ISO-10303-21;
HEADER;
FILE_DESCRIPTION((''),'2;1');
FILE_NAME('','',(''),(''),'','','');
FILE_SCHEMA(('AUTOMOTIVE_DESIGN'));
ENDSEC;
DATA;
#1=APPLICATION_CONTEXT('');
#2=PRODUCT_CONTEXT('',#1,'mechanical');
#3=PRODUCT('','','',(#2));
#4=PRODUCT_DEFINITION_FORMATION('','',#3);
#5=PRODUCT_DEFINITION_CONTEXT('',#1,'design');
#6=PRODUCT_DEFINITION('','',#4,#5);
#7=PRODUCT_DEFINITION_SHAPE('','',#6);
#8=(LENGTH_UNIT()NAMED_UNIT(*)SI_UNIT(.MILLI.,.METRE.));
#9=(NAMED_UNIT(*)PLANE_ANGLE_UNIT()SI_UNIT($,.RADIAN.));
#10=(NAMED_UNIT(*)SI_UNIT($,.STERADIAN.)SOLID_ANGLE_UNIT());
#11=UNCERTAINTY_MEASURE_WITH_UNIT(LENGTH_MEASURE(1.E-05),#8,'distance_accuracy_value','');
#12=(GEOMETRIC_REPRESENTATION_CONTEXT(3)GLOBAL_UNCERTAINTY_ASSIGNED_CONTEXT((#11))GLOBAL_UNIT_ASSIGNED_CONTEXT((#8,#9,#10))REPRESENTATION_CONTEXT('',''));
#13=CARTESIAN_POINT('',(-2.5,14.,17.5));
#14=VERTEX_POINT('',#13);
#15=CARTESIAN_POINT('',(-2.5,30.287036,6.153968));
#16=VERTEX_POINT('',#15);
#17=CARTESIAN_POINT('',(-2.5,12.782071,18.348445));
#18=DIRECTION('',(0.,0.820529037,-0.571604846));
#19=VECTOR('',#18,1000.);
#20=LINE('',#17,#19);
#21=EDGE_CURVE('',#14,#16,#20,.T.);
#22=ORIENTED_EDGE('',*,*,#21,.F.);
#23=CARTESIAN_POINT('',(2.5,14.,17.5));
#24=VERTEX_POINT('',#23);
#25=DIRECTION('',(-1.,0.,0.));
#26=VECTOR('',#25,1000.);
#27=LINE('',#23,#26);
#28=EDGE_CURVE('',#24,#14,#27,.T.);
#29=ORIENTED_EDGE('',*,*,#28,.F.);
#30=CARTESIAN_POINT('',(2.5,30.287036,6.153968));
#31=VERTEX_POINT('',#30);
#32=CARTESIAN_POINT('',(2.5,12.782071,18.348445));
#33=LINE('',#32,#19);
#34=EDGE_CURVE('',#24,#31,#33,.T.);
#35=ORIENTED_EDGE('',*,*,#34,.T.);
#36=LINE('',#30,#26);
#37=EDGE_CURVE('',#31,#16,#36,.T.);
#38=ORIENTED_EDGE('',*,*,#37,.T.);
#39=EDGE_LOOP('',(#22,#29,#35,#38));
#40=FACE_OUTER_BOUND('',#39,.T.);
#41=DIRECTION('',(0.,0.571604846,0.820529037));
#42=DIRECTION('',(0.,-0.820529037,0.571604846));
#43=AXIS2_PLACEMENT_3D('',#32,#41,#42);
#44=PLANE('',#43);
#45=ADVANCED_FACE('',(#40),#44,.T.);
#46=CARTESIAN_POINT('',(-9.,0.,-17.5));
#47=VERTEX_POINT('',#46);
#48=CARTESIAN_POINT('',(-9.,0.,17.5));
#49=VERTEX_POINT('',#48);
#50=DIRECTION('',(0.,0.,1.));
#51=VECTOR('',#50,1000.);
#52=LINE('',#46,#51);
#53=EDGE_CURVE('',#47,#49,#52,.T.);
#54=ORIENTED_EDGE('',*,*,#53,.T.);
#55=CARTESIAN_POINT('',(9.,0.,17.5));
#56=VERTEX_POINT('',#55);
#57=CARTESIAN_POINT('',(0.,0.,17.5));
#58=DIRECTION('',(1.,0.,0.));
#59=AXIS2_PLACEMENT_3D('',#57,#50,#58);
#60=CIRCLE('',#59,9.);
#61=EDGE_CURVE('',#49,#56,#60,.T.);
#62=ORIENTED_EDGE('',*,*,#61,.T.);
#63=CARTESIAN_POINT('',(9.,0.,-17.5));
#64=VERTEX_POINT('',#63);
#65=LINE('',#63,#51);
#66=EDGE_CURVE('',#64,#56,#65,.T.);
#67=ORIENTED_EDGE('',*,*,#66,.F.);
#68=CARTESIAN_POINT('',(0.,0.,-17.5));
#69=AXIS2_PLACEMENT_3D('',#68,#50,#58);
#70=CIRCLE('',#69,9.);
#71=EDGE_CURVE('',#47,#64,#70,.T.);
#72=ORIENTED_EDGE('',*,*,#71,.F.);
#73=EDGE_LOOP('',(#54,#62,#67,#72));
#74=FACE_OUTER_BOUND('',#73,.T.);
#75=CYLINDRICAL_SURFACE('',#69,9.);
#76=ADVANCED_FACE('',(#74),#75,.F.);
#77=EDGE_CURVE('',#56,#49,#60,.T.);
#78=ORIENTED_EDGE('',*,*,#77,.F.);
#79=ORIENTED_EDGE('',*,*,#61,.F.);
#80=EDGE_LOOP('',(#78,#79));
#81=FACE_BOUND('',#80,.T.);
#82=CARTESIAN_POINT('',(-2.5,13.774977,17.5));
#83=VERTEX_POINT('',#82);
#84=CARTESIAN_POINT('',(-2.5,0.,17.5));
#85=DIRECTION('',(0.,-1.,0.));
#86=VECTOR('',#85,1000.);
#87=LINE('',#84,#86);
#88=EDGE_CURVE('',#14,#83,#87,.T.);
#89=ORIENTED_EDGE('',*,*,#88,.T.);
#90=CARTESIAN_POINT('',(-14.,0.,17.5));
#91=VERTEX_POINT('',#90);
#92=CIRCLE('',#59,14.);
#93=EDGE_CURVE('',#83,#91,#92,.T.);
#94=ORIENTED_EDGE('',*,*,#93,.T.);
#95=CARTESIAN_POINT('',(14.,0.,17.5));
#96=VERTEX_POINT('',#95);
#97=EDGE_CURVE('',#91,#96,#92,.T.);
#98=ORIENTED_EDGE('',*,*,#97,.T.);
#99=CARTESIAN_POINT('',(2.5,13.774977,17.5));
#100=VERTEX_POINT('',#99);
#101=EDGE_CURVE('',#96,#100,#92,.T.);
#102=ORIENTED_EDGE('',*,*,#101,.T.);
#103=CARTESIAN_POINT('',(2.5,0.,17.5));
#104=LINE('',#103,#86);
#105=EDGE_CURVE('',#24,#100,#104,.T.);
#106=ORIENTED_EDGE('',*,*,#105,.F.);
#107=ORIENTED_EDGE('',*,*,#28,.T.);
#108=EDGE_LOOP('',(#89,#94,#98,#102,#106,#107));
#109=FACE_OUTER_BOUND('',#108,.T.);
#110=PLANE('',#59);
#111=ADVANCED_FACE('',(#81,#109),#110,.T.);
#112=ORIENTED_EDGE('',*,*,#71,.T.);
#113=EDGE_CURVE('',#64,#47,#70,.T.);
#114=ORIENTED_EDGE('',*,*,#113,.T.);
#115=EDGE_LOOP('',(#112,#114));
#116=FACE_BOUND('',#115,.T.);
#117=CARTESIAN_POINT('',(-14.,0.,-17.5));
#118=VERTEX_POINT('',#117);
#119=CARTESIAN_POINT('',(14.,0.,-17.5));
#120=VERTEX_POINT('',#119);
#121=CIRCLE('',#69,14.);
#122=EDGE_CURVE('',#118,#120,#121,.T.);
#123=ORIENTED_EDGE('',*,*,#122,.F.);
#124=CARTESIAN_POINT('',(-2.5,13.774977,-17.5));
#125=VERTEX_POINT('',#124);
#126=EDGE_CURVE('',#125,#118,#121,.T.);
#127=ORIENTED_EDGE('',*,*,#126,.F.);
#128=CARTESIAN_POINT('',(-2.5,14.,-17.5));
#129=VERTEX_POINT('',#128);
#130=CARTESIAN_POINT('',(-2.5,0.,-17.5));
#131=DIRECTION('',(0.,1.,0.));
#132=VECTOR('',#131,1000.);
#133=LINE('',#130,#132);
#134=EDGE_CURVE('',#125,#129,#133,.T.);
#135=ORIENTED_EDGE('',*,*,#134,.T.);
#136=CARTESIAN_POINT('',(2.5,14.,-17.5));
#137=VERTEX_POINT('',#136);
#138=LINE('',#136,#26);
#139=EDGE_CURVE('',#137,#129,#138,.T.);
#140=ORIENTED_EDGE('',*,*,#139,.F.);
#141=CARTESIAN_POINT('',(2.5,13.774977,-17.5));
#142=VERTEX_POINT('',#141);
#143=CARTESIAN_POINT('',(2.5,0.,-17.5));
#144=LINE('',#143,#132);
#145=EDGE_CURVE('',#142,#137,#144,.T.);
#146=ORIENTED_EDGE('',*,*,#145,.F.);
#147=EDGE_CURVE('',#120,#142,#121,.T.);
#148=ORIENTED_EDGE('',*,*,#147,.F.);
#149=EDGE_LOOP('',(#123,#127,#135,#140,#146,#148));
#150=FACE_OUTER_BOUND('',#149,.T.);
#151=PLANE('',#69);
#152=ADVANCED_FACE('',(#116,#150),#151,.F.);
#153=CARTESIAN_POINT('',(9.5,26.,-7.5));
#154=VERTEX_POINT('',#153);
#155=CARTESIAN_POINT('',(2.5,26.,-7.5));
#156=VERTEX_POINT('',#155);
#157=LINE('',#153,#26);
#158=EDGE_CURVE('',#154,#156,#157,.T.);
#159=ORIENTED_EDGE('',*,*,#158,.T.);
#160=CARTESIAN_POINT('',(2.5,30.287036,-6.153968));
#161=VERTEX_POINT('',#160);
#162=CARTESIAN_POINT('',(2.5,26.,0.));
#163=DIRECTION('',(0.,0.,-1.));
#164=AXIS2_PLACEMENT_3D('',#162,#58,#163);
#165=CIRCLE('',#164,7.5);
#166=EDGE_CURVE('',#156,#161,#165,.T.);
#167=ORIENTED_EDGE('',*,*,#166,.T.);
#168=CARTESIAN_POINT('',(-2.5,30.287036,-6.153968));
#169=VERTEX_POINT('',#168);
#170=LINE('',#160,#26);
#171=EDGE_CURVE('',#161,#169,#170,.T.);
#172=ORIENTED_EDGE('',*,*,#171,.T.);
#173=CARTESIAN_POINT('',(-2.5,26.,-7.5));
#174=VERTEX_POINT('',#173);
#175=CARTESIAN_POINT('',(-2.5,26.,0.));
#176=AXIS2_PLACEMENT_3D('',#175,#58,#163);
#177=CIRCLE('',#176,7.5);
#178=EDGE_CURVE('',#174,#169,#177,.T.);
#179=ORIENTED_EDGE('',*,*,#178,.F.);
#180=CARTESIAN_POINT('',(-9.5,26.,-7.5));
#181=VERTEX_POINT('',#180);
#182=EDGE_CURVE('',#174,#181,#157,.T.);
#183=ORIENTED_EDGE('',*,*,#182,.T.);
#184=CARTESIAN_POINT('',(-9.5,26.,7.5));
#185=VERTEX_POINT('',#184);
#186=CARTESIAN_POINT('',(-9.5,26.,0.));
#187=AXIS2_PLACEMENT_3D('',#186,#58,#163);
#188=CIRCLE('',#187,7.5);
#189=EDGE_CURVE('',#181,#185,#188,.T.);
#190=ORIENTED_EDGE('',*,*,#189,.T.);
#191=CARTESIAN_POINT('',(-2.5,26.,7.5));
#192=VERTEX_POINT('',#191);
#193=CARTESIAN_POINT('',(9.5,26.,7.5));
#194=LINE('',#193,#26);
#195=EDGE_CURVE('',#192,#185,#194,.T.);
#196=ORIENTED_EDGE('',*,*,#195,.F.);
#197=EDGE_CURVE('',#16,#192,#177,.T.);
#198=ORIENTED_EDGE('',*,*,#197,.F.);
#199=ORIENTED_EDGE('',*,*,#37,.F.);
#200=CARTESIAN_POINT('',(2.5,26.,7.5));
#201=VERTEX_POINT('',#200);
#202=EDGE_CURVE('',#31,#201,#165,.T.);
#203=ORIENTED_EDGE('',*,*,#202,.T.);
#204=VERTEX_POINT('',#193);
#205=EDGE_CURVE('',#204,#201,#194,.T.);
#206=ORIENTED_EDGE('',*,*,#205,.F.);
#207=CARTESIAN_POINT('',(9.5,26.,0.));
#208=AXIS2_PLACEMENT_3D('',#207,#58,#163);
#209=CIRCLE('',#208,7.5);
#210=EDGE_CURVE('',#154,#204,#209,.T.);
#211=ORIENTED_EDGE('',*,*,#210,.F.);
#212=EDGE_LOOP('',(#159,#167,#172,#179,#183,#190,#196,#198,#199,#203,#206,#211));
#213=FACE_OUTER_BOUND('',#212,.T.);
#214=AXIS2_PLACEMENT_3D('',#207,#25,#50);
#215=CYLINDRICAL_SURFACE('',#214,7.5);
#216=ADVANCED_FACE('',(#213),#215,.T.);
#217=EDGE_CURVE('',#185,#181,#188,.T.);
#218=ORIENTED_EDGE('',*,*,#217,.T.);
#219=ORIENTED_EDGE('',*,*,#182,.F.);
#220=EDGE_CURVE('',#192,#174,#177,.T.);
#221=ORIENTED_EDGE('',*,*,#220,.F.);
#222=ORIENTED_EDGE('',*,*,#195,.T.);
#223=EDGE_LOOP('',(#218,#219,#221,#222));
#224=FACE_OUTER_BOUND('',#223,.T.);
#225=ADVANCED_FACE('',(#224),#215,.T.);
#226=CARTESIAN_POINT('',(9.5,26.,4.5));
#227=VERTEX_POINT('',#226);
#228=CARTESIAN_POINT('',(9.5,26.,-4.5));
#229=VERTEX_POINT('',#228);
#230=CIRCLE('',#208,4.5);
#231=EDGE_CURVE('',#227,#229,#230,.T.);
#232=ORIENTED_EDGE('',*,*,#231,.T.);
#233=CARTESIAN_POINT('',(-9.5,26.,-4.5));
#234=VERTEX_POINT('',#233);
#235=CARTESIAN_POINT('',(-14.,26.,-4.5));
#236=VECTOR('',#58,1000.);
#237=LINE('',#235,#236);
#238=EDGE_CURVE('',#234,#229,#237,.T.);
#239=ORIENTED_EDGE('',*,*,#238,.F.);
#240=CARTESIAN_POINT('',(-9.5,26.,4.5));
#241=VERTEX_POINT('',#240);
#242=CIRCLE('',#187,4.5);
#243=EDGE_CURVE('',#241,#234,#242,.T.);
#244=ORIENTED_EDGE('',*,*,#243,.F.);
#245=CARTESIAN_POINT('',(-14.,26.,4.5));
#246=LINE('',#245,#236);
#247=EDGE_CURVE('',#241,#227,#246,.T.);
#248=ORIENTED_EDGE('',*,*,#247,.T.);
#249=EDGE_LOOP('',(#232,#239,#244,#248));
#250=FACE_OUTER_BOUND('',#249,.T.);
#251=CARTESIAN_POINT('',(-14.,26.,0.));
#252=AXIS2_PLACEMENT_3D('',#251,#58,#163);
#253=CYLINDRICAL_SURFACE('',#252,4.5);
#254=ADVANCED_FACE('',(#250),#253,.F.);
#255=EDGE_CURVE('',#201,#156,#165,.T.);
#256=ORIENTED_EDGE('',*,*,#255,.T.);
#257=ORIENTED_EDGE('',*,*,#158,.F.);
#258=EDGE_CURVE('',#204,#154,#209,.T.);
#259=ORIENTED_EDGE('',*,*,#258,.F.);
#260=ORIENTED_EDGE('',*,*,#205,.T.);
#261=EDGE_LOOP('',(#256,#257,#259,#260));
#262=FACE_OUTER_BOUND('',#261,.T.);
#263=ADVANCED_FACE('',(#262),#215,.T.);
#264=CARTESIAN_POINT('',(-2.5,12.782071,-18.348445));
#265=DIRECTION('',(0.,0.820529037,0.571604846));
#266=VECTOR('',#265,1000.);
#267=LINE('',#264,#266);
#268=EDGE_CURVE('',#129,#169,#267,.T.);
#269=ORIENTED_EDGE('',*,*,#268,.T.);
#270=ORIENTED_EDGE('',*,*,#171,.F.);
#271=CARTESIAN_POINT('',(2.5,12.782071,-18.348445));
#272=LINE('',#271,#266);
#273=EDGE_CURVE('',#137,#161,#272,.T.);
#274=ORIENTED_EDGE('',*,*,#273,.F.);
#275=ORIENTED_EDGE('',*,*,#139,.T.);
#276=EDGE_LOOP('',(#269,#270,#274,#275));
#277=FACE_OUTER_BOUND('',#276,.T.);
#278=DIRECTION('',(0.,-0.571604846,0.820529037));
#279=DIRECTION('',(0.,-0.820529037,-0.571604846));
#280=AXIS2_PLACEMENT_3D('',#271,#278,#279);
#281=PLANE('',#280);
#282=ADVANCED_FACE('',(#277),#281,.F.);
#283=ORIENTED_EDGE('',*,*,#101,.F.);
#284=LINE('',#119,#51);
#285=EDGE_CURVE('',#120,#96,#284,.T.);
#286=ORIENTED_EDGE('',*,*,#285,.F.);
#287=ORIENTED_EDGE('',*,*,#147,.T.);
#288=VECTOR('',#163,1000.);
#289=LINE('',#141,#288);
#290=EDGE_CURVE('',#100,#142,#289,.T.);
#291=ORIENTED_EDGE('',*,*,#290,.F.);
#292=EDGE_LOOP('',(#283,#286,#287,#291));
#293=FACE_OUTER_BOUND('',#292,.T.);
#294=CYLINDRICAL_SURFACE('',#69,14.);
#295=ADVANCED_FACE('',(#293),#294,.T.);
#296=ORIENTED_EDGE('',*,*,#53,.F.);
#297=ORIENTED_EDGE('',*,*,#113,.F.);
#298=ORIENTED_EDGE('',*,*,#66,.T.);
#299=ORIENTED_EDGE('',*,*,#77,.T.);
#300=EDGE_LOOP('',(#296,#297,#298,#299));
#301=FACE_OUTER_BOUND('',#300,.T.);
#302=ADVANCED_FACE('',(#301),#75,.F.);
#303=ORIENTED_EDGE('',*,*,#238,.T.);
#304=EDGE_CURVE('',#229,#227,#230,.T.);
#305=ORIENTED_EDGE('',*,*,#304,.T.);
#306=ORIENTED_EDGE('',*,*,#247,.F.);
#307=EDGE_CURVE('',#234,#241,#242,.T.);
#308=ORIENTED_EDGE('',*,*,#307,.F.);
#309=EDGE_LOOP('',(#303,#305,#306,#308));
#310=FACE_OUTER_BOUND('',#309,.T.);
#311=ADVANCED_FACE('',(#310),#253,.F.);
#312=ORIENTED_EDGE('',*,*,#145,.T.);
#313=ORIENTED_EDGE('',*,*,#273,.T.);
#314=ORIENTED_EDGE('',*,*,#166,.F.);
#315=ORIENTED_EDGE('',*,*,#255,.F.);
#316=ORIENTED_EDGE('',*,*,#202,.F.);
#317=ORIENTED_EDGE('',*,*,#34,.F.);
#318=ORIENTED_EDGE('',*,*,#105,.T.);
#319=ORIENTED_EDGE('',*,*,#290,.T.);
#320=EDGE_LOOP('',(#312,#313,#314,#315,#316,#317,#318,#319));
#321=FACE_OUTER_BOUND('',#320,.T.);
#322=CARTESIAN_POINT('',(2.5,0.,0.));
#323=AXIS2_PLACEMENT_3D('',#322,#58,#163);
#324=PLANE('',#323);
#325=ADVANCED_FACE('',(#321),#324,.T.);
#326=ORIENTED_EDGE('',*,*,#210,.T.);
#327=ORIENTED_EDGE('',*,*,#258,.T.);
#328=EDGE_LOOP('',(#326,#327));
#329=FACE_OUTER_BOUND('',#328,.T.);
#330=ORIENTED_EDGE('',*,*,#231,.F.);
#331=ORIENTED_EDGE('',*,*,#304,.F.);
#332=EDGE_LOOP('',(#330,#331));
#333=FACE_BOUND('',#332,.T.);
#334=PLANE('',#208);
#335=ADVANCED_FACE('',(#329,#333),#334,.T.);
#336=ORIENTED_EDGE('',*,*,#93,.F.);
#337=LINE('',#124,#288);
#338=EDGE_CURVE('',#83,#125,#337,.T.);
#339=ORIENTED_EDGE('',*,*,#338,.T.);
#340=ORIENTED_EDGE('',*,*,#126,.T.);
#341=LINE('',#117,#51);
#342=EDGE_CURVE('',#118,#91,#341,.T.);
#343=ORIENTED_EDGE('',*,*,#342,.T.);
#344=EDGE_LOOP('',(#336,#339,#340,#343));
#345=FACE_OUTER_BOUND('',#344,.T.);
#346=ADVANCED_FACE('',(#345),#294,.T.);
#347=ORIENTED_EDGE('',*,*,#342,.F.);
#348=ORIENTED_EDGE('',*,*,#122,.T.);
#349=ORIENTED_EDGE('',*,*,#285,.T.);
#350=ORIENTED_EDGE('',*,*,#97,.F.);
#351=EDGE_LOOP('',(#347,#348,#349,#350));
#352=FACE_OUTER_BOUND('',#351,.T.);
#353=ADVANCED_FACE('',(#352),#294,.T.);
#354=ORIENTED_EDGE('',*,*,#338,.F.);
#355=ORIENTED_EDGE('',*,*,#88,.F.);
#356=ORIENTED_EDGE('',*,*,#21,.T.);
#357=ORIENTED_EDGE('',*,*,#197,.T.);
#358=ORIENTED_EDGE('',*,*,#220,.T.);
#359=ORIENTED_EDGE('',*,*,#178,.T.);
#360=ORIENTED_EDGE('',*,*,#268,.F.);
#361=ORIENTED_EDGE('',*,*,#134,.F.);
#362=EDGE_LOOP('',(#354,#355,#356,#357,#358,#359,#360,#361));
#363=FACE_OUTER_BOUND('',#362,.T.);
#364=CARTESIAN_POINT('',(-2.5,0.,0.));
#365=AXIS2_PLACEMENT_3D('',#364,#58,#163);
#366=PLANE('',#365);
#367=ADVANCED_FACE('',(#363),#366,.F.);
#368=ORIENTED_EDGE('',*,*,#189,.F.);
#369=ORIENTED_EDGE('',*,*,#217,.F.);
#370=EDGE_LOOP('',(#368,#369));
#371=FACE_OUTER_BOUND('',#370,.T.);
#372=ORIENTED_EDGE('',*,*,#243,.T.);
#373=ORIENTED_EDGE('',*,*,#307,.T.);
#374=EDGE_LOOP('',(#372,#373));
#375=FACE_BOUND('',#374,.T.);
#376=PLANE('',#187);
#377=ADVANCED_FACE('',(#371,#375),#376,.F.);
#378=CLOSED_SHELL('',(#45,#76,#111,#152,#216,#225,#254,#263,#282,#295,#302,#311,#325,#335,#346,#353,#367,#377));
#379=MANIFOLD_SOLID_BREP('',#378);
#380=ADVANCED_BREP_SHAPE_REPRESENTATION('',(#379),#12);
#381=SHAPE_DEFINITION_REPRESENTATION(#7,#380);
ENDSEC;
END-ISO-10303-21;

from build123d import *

# Parameters (mm, degrees)
MAIN_BARREL_28_DEPTH      = 17.5
MAIN_BARREL_28_DEPTH_BACK = 17.5
MAIN_BARREL_SKETCH_R      = 14
MAIN_BORE_SKETCH_R        = 9
MAIN_BORE_18_DEPTH        = 41.211938526
UPPER_BOSS_SKETCH_R       = 7.5
UPPER_BOSS_15_DEPTH       = 9.5
UPPER_BORE_SKETCH_R       = 4.5
UPPER_BORE_9_DEPTH        = 45.505617623
CONNECTING_WEB_DEPTH      = 2.5


with BuildPart() as part:
    # Main Barrel Sketch → Main Barrel _28 (new, two sides: drawn at the far end of the back side and taken through both)
    with BuildSketch(Plane.XY.offset(-MAIN_BARREL_28_DEPTH_BACK)):
        Circle(MAIN_BARREL_SKETCH_R)
    extrude(amount=MAIN_BARREL_28_DEPTH + MAIN_BARREL_28_DEPTH_BACK)

    # Main Bore Sketch → Main Bore _18 (cut, through all)
    with BuildSketch(Plane.XY.offset(17.5)):
        Circle(MAIN_BORE_SKETCH_R)
    extrude(amount=-MAIN_BORE_18_DEPTH, mode=Mode.SUBTRACT)



with BuildPart() as body_2:
    # Upper Boss Sketch → Upper Boss _15 (new, symmetric)
    with BuildSketch(Plane(origin=(0, 0, 0), x_dir=(0, 0, -1), z_dir=(1, 0, 0))):
        with Locations((0, 26)):
            Circle(UPPER_BOSS_SKETCH_R)
    extrude(amount=UPPER_BOSS_15_DEPTH, both=True)

    # Upper Bore Sketch → Upper Bore _9 (cut, through all)
    with BuildSketch(Plane(origin=(9.5, 0, 0), x_dir=(0, 0, -1), z_dir=(1, 0, 0))):
        with Locations((0, 26)):
            Circle(UPPER_BORE_SKETCH_R)
    extrude(amount=-UPPER_BORE_9_DEPTH, mode=Mode.SUBTRACT)


with BuildPart() as part_1:
    add(part.part)

    add(body_2.part)  # Connecting Web merges body 2
    # Web Sketch → Connecting Web (add, symmetric)
    with BuildSketch(Plane(origin=(0, 0, 0), x_dir=(0, 0, -1), z_dir=(1, 0, 0))):
        with BuildLine():
            Line((-6.153967777, 30.287036342), (-17.5, 14))
            Line((-17.5, 14), (-17.5, 13))
            Line((-17.5, 13), (17.5, 13))
            Line((17.5, 13), (17.5, 14))
            Line((17.5, 14), (6.153967777, 30.287036342))
            ThreePointArc((6.153967777, 30.287036342), (7.155583775, 28.246691086), (7.5, 26))
            ThreePointArc((7.5, 26), (-2.246691086, 18.844416225), (-6.153967777, 30.287036342))
        make_face()
    extrude(amount=CONNECTING_WEB_DEPTH, both=True)


solid = part_1.part
